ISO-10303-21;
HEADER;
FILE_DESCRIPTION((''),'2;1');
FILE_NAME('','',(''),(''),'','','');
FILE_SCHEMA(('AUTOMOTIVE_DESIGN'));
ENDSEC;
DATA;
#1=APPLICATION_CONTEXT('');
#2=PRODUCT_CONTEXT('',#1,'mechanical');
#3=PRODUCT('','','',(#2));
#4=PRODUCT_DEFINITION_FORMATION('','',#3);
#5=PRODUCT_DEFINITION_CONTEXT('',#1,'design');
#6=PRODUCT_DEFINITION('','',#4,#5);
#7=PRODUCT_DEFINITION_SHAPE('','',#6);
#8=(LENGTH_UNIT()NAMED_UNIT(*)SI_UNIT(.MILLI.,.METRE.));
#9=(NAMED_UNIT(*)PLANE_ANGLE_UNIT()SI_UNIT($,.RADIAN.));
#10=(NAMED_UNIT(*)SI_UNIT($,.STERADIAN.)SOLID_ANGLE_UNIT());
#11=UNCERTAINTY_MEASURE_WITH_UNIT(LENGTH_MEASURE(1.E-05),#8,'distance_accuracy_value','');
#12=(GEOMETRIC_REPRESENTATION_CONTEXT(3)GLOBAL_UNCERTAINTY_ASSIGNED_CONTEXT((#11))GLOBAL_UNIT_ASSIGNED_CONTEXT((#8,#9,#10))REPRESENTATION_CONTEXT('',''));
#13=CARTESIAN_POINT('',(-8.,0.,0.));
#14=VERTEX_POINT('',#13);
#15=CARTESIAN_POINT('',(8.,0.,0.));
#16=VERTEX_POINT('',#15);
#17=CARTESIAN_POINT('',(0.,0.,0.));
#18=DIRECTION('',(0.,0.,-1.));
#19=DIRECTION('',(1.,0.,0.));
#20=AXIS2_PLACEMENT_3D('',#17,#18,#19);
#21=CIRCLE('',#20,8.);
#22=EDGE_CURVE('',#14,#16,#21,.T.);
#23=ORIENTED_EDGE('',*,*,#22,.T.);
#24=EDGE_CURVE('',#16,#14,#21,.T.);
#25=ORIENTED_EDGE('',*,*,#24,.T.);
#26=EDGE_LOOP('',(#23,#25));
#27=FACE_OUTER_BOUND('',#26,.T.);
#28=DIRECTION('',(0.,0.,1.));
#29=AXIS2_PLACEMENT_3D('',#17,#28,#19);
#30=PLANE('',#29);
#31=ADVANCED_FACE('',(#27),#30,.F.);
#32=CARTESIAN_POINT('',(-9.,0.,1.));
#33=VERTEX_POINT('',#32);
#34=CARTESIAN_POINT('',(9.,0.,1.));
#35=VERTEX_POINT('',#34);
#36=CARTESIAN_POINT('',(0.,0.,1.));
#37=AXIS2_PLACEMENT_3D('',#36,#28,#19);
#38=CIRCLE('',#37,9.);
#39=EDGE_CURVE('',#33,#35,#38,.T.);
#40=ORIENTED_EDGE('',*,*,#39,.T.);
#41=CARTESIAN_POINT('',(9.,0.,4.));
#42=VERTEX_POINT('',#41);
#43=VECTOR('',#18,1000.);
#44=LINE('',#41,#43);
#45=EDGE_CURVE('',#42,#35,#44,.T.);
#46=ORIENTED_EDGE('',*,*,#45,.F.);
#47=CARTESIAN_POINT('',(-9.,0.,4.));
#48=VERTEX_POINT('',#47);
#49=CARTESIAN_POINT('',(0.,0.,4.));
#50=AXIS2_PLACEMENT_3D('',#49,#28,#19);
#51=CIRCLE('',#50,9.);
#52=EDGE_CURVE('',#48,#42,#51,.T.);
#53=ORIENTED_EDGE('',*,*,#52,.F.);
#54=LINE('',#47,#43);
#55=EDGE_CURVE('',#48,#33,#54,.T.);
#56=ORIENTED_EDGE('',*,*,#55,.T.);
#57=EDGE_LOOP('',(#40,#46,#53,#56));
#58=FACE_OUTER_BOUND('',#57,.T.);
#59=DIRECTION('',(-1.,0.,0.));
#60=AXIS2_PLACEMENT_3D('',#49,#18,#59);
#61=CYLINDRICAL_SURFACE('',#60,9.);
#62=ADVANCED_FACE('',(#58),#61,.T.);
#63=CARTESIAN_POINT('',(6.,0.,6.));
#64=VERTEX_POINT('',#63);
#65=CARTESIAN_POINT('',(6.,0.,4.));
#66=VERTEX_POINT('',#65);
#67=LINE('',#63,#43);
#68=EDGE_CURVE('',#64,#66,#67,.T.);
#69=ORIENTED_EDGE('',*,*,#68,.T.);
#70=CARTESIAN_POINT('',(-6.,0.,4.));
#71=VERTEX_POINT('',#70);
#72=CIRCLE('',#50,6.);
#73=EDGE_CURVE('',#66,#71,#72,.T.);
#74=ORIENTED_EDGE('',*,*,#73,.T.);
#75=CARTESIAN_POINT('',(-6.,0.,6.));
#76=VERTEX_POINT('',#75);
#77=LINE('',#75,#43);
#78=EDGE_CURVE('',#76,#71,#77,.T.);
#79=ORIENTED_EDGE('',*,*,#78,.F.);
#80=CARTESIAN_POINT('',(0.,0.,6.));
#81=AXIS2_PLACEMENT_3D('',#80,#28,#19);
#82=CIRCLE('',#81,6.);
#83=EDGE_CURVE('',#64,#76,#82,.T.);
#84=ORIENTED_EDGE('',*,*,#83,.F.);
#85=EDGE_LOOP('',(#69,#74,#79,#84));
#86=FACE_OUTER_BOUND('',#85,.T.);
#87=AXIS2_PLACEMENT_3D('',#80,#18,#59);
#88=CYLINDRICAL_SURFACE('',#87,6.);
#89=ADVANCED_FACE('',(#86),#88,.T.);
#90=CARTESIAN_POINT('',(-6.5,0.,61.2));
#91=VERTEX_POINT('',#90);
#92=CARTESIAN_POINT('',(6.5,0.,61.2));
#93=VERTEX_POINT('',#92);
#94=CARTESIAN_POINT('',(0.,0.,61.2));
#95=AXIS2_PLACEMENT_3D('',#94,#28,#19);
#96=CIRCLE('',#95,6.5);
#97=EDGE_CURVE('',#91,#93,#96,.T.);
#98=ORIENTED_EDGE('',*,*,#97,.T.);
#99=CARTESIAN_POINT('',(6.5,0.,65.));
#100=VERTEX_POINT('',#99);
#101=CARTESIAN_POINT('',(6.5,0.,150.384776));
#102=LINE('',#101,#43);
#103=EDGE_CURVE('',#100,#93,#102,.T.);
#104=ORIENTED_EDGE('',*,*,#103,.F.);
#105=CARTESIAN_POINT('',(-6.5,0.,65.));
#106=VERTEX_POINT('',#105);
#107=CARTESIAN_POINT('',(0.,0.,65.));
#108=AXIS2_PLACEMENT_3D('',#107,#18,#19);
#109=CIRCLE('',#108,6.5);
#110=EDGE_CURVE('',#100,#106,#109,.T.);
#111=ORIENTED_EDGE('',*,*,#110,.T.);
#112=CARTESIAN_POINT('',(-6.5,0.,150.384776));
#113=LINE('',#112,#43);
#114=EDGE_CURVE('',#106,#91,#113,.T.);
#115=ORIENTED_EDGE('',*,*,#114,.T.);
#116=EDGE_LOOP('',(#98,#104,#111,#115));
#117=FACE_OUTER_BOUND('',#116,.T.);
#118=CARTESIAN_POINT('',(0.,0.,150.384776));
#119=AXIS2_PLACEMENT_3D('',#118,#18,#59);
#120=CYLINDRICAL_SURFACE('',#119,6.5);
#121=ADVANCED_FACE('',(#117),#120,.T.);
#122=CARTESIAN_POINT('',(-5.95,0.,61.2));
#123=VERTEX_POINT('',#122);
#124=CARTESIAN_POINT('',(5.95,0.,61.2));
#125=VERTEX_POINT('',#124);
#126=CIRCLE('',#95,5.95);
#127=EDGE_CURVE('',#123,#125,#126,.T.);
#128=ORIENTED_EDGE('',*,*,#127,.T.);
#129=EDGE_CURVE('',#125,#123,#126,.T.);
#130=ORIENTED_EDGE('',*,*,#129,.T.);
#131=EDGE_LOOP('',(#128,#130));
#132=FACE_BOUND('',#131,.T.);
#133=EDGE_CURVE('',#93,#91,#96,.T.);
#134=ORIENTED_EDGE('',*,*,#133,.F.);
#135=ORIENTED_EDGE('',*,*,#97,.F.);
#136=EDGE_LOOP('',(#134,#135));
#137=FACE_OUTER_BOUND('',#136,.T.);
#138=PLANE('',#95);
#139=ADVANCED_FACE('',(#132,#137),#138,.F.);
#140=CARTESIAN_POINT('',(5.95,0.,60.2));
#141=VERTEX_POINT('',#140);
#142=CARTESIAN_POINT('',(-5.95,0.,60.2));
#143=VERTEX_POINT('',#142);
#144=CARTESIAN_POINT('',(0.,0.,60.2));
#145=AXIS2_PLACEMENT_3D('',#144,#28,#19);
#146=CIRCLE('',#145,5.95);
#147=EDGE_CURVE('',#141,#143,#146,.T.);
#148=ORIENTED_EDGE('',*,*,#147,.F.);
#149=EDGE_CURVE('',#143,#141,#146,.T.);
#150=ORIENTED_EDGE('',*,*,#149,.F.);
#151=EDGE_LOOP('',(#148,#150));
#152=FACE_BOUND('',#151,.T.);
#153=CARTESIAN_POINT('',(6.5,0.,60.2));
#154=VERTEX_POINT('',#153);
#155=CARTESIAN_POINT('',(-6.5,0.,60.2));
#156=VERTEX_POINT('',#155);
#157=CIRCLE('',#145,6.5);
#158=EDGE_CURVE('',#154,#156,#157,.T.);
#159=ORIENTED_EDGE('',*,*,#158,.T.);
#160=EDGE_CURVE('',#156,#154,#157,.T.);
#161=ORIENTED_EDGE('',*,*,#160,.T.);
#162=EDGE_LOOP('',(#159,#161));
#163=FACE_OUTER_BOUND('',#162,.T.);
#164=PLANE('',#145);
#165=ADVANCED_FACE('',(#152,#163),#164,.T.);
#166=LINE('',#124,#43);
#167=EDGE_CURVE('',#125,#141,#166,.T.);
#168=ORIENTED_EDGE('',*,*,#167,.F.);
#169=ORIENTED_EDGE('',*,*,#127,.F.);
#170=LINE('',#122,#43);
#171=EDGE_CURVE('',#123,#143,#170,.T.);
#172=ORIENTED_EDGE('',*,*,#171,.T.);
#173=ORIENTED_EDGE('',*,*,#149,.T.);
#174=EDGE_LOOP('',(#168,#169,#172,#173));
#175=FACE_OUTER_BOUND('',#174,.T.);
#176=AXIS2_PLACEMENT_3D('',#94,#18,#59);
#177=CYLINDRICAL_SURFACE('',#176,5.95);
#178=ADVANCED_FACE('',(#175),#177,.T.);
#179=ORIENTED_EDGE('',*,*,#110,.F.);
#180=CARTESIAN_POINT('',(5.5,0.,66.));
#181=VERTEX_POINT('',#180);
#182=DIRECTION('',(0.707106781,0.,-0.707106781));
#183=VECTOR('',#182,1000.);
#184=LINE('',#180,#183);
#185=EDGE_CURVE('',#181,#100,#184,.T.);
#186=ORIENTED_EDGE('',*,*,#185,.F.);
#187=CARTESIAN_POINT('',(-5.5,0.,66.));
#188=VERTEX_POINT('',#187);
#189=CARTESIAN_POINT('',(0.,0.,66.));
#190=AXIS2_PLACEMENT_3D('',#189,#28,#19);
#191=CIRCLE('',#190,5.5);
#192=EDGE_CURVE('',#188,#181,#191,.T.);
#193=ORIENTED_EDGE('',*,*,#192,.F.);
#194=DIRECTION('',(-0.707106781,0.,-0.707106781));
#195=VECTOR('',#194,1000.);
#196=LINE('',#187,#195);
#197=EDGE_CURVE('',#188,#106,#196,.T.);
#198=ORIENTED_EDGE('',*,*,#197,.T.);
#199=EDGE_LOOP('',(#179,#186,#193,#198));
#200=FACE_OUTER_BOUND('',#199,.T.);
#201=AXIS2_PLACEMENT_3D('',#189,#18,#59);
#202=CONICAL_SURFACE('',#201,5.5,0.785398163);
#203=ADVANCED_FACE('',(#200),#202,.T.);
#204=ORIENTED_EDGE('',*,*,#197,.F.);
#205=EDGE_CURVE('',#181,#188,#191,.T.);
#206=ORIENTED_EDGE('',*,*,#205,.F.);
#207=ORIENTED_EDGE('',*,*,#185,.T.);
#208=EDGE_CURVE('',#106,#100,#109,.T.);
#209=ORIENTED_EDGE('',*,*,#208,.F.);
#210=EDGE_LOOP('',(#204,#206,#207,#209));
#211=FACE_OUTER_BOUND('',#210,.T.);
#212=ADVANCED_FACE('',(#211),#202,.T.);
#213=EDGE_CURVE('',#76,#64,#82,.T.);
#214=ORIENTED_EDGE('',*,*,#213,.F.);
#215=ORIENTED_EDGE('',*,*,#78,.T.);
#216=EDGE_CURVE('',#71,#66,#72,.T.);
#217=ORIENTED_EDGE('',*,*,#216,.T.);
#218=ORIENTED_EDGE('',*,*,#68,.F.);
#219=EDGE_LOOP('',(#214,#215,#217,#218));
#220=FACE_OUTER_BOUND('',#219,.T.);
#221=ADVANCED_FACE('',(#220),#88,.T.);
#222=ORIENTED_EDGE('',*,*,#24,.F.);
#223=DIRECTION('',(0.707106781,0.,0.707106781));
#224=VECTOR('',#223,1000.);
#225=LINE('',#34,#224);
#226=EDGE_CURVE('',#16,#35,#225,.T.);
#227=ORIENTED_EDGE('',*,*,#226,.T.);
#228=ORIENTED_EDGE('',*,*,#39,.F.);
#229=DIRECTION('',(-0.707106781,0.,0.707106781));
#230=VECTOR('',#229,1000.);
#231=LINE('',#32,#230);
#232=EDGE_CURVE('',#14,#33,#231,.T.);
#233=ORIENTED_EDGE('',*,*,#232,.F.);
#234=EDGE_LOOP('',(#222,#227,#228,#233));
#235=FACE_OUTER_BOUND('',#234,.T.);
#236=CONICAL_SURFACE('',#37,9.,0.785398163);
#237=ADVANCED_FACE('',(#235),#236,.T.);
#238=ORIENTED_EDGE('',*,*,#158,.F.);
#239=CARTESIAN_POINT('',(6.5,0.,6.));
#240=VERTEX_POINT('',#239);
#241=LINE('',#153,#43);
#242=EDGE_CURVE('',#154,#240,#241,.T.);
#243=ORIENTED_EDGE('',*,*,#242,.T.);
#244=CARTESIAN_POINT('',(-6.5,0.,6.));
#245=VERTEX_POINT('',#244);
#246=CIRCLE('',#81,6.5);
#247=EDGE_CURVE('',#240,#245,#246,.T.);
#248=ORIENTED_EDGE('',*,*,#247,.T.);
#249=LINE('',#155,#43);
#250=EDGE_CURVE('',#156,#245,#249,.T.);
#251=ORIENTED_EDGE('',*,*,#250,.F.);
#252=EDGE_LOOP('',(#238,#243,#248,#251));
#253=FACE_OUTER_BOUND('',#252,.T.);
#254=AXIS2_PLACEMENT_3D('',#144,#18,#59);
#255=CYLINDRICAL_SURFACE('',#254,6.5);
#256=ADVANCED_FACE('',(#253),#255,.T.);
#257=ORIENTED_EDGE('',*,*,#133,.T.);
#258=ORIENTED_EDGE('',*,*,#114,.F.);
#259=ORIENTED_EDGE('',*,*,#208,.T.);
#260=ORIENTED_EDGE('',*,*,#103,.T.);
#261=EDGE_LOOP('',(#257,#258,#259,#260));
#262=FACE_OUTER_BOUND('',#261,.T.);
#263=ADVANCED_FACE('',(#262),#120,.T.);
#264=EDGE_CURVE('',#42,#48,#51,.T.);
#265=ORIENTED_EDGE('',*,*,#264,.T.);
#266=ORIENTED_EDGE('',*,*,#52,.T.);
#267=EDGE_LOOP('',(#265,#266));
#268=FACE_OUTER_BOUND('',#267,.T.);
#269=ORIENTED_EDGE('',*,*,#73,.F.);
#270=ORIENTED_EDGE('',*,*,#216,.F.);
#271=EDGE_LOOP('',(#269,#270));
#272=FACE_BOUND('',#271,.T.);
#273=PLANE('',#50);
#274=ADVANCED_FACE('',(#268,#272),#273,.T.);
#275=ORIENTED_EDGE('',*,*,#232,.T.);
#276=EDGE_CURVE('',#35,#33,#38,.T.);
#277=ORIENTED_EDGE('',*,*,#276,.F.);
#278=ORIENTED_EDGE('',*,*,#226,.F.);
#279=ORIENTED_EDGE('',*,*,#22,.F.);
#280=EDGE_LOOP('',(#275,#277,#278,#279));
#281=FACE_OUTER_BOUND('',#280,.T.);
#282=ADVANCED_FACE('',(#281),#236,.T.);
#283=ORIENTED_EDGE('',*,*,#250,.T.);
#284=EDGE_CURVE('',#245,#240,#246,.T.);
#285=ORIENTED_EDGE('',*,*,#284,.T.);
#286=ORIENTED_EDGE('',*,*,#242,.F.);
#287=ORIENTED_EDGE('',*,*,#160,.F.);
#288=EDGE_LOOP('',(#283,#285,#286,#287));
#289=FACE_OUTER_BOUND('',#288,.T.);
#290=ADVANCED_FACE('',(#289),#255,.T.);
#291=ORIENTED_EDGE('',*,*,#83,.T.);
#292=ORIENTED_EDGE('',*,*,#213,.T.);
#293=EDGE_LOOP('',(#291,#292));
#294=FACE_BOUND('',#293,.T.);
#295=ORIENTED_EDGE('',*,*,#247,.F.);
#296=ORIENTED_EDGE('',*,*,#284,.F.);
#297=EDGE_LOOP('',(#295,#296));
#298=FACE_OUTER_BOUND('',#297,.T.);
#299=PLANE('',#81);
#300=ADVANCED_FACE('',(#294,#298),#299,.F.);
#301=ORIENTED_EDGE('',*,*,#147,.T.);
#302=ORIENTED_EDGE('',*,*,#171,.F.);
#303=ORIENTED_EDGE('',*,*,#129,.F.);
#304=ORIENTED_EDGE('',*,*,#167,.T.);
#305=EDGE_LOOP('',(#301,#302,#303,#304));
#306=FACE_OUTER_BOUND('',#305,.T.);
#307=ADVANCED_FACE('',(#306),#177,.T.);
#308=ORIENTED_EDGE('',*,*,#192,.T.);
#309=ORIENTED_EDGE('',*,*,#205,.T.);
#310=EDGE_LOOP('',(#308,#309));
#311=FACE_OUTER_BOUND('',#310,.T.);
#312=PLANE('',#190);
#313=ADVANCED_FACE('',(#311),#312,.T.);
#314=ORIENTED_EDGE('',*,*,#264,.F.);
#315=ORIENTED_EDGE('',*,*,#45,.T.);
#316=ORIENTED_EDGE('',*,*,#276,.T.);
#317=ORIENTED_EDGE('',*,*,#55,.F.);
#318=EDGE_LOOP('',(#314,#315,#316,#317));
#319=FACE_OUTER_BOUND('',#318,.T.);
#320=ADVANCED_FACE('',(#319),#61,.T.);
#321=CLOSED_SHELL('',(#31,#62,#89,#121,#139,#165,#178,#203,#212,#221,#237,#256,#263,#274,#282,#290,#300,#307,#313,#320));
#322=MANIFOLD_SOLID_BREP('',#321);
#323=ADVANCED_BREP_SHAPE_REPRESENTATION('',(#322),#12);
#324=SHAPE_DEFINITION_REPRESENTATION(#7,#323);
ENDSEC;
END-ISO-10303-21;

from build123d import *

# Parameters (mm, degrees)
SKETCH1_R           = 9
BOSS_EXTRUDE1_DEPTH = 4
SKETCH2_R           = 6
BOSS_EXTRUDE2_DEPTH = 2
SKETCH3_R           = 6.5
BOSS_EXTRUDE3_DEPTH = 54.2
SKETCH4_R           = 5.95
BOSS_EXTRUDE4_DEPTH = 1
SKETCH5_R           = 6.5
BOSS_EXTRUDE5_DEPTH = 4.8
CHAMFER1_SIZE       = 1


with BuildPart() as part:
    # Sketch1 → Boss-Extrude1 (new body)
    with BuildSketch(Plane.XY):
        Circle(SKETCH1_R)
    extrude(amount=BOSS_EXTRUDE1_DEPTH)

    # Sketch2 → Boss-Extrude2 (add)
    with BuildSketch(Plane.XY.offset(4)):
        Circle(SKETCH2_R)
    extrude(amount=BOSS_EXTRUDE2_DEPTH)

    # Sketch3 → Boss-Extrude3 (add)
    with BuildSketch(Plane.XY.offset(6)):
        with Locations(Location((0, 0, 0), (0, 0, 180))):
            Circle(SKETCH3_R)
    extrude(amount=BOSS_EXTRUDE3_DEPTH)

    # Sketch4 → Boss-Extrude4 (add)
    with BuildSketch(Plane.XY.offset(60.2)):
        Circle(SKETCH4_R)
    extrude(amount=BOSS_EXTRUDE4_DEPTH)

    # Sketch5 → Boss-Extrude5 (add)
    with BuildSketch(Plane.XY.offset(61.2)):
        with Locations(Location((0, 0, 0), (0, 0, 180))):
            Circle(SKETCH5_R)
    extrude(amount=BOSS_EXTRUDE5_DEPTH)

    # Chamfer1
    chamfer1_edges = [part.edges().sort_by_distance(p)[0] for p in [
        (-9, 0, 0),
        (6.5, 0, 66),
    ]]
    chamfer(chamfer1_edges, length=CHAMFER1_SIZE)


solid = part.part
